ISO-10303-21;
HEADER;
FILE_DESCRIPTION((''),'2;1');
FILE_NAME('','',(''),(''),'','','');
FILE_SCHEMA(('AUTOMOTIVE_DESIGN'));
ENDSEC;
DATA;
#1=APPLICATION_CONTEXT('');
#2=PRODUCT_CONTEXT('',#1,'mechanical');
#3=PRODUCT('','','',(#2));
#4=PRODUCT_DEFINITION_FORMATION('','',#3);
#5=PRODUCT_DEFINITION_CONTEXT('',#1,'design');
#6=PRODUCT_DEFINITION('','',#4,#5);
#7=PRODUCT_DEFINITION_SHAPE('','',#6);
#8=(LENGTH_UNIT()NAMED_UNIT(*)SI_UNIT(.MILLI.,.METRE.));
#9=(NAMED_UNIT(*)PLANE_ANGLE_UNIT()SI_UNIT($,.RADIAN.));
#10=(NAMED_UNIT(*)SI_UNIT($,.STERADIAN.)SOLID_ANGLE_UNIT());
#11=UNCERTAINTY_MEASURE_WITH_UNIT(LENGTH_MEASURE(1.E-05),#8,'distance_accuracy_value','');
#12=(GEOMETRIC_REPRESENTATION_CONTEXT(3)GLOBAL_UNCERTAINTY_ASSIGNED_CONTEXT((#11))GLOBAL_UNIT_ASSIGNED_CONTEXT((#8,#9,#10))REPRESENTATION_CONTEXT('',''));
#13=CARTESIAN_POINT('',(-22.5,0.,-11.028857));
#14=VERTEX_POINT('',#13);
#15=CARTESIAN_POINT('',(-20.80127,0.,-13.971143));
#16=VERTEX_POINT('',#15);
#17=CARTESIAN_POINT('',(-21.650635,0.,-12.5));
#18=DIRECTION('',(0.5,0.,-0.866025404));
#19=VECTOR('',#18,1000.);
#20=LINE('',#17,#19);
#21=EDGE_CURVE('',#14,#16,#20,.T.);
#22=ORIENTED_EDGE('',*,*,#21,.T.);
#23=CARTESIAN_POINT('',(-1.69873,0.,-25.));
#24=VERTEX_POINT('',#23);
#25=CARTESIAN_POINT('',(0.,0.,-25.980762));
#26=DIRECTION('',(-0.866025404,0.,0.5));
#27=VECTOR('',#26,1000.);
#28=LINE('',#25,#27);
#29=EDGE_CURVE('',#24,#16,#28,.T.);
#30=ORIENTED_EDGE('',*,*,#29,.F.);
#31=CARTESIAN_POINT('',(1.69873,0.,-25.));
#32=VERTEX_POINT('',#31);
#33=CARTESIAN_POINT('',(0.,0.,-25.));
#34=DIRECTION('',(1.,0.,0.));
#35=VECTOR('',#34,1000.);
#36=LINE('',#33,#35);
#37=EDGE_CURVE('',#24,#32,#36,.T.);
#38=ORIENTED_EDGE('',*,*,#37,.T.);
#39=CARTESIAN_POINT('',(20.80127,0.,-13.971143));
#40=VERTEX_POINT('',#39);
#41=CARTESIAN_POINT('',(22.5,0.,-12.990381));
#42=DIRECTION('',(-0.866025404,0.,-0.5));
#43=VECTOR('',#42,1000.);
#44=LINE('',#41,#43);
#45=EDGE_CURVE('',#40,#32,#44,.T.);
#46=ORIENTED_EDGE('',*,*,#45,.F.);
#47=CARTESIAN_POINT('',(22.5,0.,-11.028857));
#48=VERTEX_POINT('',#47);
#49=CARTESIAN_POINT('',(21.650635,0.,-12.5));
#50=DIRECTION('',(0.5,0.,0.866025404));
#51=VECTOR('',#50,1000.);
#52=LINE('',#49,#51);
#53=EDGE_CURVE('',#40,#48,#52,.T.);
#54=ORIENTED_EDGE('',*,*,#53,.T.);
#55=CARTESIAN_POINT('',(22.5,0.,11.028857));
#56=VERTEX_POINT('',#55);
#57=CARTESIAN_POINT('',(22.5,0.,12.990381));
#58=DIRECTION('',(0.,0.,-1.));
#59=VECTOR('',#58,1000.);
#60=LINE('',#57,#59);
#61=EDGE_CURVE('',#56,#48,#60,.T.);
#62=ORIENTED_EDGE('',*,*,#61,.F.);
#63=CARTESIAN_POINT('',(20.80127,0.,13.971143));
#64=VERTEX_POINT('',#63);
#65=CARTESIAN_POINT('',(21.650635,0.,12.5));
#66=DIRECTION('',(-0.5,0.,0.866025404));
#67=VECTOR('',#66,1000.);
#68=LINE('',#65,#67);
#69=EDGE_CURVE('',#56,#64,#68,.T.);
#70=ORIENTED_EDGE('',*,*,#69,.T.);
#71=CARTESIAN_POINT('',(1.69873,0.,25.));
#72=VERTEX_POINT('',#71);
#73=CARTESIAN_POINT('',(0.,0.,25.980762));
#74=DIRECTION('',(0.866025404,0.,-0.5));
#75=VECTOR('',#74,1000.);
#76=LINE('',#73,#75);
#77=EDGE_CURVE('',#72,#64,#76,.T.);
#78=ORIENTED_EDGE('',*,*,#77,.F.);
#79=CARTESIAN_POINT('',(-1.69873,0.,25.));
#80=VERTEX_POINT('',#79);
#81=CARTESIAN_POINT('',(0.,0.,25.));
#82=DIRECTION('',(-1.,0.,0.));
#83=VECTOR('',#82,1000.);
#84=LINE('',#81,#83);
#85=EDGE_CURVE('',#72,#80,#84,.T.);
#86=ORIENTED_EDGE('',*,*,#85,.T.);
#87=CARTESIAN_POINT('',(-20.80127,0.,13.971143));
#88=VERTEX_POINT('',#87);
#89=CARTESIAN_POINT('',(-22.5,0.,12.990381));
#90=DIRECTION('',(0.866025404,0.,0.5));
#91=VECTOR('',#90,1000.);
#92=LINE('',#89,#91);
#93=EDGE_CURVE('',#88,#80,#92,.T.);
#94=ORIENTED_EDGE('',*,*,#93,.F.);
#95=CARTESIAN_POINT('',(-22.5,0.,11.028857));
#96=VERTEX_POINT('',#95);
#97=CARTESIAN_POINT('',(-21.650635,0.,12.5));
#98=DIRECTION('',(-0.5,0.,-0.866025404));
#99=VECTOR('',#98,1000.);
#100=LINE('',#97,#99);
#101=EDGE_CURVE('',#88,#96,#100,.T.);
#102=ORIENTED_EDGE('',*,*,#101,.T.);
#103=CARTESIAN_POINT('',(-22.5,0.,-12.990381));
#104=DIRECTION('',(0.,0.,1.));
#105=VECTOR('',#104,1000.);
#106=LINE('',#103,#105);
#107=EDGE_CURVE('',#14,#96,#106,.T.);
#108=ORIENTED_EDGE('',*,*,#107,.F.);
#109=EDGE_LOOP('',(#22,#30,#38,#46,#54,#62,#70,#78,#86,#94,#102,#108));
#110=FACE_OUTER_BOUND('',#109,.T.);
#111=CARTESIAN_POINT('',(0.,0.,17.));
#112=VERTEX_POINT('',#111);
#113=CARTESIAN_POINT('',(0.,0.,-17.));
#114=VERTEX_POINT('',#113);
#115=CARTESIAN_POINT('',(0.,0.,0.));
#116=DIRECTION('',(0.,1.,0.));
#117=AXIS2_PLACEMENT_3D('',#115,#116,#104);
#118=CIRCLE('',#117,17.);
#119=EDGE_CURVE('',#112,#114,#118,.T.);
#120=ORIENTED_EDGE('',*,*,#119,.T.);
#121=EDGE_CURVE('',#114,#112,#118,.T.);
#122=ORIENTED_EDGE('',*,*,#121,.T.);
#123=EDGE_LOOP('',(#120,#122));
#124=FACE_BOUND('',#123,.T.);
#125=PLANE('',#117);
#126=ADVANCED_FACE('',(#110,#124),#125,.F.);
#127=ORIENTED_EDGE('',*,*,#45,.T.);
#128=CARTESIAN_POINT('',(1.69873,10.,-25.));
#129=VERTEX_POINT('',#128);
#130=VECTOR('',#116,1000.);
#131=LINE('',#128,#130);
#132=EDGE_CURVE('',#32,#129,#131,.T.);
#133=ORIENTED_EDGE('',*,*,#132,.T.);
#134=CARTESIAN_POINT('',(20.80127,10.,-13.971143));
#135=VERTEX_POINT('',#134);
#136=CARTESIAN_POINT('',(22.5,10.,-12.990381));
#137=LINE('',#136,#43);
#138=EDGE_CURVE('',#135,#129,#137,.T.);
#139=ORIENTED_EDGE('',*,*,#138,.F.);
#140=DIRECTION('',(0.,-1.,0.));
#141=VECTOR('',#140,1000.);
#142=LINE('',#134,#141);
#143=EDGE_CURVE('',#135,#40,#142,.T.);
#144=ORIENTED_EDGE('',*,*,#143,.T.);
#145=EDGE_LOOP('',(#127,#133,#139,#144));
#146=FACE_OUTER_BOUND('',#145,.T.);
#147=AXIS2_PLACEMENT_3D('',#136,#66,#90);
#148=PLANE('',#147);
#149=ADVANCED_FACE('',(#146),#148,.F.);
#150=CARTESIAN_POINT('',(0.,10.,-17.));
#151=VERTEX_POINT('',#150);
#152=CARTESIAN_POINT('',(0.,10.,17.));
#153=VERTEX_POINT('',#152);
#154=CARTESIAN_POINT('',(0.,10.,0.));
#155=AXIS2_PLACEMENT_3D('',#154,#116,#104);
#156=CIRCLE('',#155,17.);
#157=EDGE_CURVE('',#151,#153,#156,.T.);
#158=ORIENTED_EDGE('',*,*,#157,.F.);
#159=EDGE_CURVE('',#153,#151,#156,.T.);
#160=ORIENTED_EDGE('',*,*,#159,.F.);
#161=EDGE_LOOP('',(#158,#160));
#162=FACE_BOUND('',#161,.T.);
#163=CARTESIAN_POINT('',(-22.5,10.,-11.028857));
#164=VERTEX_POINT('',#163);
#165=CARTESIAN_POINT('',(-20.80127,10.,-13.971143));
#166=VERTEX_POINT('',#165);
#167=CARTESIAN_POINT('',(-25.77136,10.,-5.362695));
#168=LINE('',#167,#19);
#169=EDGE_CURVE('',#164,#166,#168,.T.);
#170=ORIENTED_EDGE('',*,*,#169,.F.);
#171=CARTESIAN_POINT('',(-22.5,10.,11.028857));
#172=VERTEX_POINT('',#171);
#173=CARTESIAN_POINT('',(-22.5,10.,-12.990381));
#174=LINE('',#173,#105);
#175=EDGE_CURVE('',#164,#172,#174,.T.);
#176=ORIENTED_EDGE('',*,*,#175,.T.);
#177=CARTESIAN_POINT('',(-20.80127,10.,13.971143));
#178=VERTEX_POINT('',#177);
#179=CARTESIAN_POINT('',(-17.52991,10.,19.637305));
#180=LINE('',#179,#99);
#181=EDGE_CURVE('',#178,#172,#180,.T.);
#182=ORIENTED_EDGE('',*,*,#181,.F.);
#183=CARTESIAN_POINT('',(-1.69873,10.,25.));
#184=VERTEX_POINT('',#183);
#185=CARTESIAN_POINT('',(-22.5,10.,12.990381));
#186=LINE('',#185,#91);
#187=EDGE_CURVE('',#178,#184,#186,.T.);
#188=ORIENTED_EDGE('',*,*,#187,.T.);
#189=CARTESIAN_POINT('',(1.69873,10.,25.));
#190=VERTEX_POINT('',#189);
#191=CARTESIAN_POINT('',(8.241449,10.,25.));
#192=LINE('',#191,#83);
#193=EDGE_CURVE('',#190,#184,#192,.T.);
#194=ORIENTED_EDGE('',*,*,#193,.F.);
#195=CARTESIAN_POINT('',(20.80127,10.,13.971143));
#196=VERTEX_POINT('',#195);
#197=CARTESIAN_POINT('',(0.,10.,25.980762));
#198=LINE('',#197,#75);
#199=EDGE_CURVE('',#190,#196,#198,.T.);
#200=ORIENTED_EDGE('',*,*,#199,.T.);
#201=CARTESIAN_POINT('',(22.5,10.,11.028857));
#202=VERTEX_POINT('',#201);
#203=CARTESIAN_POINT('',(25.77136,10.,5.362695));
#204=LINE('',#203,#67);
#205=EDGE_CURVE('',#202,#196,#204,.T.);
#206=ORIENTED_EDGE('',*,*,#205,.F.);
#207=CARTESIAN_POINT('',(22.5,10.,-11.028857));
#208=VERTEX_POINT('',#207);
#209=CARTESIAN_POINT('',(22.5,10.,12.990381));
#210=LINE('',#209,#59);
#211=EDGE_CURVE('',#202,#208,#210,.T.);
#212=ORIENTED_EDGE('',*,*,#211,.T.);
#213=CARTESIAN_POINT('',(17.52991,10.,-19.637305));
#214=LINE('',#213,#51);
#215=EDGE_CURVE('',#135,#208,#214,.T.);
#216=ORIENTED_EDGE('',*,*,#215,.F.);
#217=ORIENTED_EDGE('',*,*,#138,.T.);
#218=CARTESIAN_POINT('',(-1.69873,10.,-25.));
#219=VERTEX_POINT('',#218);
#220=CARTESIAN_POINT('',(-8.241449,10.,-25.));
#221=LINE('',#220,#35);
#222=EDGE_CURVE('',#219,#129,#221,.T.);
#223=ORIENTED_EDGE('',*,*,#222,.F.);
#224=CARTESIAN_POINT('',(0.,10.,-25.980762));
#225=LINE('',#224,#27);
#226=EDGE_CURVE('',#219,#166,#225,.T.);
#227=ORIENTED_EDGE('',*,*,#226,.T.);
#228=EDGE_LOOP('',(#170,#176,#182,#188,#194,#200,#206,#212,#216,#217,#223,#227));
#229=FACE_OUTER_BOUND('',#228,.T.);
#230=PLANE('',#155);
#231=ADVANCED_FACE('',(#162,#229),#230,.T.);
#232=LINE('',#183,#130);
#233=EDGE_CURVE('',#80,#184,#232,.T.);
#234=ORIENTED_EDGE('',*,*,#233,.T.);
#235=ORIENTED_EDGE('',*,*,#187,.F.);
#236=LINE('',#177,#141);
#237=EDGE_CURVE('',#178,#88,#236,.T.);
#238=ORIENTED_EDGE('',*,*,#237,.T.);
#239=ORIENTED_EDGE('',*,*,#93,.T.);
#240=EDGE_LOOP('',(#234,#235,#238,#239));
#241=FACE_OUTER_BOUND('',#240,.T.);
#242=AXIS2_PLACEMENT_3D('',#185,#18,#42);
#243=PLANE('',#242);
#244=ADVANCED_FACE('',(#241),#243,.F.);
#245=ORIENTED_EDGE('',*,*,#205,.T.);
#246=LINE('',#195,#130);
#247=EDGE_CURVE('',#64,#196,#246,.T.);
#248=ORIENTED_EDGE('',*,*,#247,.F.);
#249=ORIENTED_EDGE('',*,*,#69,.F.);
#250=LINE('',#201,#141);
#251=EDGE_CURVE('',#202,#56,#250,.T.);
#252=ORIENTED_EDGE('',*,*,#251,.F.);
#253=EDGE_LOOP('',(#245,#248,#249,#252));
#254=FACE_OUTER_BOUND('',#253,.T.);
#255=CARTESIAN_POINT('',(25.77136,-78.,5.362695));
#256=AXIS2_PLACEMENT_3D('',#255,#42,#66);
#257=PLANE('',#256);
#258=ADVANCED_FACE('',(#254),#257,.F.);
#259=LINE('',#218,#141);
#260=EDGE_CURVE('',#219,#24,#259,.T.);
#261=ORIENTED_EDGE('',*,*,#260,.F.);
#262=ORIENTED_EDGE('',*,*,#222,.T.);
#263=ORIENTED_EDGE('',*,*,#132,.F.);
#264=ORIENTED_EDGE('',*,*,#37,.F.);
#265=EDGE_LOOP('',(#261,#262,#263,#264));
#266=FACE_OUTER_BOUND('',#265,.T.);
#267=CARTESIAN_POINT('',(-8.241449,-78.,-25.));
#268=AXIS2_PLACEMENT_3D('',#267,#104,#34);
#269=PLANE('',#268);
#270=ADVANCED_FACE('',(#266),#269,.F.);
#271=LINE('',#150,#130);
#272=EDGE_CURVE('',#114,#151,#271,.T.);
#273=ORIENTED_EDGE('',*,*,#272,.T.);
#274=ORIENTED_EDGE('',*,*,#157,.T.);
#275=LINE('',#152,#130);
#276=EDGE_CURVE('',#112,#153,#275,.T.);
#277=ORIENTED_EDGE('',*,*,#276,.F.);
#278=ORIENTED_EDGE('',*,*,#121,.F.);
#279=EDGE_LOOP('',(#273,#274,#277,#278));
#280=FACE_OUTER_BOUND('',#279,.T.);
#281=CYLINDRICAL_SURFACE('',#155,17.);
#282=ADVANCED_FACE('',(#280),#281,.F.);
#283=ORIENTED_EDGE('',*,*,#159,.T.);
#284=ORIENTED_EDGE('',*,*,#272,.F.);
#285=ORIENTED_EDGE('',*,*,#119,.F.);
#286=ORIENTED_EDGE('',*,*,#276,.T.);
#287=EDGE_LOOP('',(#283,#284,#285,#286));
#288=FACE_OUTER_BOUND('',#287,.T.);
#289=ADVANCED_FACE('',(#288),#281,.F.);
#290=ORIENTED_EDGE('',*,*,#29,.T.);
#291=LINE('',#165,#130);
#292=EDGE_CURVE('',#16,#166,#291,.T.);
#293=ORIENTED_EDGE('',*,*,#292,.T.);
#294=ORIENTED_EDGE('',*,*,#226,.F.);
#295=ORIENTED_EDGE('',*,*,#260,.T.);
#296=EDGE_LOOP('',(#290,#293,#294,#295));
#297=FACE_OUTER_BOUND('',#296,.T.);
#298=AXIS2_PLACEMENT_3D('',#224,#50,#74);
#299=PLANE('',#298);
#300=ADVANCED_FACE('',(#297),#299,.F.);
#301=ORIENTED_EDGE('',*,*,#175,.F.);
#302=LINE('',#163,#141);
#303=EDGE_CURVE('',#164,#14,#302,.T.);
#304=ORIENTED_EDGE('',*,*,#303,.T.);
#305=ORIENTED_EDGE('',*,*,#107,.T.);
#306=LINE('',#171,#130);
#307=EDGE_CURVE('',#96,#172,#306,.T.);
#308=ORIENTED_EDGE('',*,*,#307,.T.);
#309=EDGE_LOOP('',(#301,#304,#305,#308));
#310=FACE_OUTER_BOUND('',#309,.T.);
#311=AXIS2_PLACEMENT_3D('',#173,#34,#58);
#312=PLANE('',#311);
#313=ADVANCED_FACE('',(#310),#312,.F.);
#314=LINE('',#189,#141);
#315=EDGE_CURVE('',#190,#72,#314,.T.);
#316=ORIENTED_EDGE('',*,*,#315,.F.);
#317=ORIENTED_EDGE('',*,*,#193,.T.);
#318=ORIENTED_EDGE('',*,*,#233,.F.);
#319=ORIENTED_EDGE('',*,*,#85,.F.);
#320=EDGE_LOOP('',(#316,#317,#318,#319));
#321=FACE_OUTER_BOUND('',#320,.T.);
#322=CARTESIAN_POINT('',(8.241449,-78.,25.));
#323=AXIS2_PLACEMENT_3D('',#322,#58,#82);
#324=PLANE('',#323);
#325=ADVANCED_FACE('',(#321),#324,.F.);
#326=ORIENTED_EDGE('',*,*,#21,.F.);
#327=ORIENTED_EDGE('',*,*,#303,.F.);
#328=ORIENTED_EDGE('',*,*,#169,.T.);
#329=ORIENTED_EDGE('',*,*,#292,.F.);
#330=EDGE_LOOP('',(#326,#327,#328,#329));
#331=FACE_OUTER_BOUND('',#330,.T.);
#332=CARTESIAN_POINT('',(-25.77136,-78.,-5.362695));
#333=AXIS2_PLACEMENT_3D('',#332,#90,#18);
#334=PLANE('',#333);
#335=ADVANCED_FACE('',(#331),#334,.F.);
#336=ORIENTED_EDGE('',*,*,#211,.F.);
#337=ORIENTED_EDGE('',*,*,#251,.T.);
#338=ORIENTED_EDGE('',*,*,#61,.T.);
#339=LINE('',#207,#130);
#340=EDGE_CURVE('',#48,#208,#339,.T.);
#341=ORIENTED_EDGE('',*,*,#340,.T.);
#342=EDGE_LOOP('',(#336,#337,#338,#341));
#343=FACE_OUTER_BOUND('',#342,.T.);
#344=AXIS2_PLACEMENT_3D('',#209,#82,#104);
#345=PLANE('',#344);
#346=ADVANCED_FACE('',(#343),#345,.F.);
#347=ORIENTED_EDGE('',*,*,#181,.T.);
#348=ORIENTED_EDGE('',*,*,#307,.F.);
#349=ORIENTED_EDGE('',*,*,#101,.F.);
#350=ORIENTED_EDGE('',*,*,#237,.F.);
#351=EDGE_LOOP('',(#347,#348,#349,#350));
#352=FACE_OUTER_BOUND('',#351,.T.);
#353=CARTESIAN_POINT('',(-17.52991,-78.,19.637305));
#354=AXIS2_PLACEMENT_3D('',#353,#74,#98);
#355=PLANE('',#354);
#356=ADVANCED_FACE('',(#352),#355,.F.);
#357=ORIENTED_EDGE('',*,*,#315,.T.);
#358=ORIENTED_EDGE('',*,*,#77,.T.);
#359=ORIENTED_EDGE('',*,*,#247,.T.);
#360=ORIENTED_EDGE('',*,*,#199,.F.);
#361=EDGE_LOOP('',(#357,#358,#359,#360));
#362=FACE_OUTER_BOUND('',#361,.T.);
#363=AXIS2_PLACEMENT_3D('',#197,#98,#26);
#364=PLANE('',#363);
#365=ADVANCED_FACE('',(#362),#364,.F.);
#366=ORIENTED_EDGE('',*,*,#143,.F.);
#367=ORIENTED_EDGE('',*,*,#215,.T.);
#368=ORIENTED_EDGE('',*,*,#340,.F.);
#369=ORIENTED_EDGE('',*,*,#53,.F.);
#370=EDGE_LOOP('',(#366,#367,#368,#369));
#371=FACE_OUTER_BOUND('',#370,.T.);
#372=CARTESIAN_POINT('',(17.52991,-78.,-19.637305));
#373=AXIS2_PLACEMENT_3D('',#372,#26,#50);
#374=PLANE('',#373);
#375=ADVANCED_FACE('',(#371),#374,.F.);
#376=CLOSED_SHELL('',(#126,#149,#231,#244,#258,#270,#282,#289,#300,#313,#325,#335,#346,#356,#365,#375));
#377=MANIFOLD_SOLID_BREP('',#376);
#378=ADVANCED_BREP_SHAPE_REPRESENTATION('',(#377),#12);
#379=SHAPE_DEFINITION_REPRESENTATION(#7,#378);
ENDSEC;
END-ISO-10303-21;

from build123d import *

# Parameters (mm, degrees)
BOSS_EXTRUDE1_DEPTH        = 10
M36X2_0_TAPPED_HOLE1_D     = 34
M36X2_0_TAPPED_HOLE1_DEPTH = 82
M36X2_0_TAPPED_HOLE1_TIP   = 10.214630523
SKETCH4_W                  = 19.309531336
SKETCH4_H                  = 7.869851007
CUT_EXTRUDE1_DEPTH         = 88
CIRPATTERN1_COUNT          = 6


with BuildPart() as part:
    # Sketch1 → Boss-Extrude1 (new body)
    with BuildSketch(Plane(origin=(0, 0, 0), x_dir=(1, 0, 0), z_dir=(0, 1, 0))):
        Polygon((22.5, -12.990381057), (22.5, 12.990381057), (0, 25.980762114), (-22.5, 12.990381057), (-22.5, -12.990381057), (0, -25.980762114), align=None)
    extrude(amount=BOSS_EXTRUDE1_DEPTH)

    # M36x2.0 Tapped Hole1
    with Locations(Plane(origin=(0, 10, 0), x_dir=(1, 0, 0), z_dir=(0, 1, 0))):
        with Locations((0, 0)):
            Hole(M36X2_0_TAPPED_HOLE1_D / 2, depth=M36X2_0_TAPPED_HOLE1_DEPTH)
            with Locations((0, 0, -(M36X2_0_TAPPED_HOLE1_DEPTH + M36X2_0_TAPPED_HOLE1_TIP / 2))):  # 118° drill point
                Cone(0, M36X2_0_TAPPED_HOLE1_D / 2, M36X2_0_TAPPED_HOLE1_TIP, mode=Mode.SUBTRACT)

    # Sketch4 → Cut-Extrude1 (cut)
    with BuildSketch(Plane(origin=(0, 10, 0), x_dir=(1, 0, 0), z_dir=(0, 1, 0))):
        with Locations((1.413316262, 28.934925504)):
            Rectangle(SKETCH4_W, SKETCH4_H)
    cut_extrude1 = extrude(amount=-CUT_EXTRUDE1_DEPTH, mode=Mode.SUBTRACT)

    # CirPattern1: Cut-Extrude1 ×6 about axis
    cirpattern1_axis = Axis((0, 0, 0), (0, 1, 0))
    for i in range(1, CIRPATTERN1_COUNT):
        add(cut_extrude1.rotate(cirpattern1_axis, i * 360 / CIRPATTERN1_COUNT), mode=Mode.SUBTRACT)


solid = part.part
